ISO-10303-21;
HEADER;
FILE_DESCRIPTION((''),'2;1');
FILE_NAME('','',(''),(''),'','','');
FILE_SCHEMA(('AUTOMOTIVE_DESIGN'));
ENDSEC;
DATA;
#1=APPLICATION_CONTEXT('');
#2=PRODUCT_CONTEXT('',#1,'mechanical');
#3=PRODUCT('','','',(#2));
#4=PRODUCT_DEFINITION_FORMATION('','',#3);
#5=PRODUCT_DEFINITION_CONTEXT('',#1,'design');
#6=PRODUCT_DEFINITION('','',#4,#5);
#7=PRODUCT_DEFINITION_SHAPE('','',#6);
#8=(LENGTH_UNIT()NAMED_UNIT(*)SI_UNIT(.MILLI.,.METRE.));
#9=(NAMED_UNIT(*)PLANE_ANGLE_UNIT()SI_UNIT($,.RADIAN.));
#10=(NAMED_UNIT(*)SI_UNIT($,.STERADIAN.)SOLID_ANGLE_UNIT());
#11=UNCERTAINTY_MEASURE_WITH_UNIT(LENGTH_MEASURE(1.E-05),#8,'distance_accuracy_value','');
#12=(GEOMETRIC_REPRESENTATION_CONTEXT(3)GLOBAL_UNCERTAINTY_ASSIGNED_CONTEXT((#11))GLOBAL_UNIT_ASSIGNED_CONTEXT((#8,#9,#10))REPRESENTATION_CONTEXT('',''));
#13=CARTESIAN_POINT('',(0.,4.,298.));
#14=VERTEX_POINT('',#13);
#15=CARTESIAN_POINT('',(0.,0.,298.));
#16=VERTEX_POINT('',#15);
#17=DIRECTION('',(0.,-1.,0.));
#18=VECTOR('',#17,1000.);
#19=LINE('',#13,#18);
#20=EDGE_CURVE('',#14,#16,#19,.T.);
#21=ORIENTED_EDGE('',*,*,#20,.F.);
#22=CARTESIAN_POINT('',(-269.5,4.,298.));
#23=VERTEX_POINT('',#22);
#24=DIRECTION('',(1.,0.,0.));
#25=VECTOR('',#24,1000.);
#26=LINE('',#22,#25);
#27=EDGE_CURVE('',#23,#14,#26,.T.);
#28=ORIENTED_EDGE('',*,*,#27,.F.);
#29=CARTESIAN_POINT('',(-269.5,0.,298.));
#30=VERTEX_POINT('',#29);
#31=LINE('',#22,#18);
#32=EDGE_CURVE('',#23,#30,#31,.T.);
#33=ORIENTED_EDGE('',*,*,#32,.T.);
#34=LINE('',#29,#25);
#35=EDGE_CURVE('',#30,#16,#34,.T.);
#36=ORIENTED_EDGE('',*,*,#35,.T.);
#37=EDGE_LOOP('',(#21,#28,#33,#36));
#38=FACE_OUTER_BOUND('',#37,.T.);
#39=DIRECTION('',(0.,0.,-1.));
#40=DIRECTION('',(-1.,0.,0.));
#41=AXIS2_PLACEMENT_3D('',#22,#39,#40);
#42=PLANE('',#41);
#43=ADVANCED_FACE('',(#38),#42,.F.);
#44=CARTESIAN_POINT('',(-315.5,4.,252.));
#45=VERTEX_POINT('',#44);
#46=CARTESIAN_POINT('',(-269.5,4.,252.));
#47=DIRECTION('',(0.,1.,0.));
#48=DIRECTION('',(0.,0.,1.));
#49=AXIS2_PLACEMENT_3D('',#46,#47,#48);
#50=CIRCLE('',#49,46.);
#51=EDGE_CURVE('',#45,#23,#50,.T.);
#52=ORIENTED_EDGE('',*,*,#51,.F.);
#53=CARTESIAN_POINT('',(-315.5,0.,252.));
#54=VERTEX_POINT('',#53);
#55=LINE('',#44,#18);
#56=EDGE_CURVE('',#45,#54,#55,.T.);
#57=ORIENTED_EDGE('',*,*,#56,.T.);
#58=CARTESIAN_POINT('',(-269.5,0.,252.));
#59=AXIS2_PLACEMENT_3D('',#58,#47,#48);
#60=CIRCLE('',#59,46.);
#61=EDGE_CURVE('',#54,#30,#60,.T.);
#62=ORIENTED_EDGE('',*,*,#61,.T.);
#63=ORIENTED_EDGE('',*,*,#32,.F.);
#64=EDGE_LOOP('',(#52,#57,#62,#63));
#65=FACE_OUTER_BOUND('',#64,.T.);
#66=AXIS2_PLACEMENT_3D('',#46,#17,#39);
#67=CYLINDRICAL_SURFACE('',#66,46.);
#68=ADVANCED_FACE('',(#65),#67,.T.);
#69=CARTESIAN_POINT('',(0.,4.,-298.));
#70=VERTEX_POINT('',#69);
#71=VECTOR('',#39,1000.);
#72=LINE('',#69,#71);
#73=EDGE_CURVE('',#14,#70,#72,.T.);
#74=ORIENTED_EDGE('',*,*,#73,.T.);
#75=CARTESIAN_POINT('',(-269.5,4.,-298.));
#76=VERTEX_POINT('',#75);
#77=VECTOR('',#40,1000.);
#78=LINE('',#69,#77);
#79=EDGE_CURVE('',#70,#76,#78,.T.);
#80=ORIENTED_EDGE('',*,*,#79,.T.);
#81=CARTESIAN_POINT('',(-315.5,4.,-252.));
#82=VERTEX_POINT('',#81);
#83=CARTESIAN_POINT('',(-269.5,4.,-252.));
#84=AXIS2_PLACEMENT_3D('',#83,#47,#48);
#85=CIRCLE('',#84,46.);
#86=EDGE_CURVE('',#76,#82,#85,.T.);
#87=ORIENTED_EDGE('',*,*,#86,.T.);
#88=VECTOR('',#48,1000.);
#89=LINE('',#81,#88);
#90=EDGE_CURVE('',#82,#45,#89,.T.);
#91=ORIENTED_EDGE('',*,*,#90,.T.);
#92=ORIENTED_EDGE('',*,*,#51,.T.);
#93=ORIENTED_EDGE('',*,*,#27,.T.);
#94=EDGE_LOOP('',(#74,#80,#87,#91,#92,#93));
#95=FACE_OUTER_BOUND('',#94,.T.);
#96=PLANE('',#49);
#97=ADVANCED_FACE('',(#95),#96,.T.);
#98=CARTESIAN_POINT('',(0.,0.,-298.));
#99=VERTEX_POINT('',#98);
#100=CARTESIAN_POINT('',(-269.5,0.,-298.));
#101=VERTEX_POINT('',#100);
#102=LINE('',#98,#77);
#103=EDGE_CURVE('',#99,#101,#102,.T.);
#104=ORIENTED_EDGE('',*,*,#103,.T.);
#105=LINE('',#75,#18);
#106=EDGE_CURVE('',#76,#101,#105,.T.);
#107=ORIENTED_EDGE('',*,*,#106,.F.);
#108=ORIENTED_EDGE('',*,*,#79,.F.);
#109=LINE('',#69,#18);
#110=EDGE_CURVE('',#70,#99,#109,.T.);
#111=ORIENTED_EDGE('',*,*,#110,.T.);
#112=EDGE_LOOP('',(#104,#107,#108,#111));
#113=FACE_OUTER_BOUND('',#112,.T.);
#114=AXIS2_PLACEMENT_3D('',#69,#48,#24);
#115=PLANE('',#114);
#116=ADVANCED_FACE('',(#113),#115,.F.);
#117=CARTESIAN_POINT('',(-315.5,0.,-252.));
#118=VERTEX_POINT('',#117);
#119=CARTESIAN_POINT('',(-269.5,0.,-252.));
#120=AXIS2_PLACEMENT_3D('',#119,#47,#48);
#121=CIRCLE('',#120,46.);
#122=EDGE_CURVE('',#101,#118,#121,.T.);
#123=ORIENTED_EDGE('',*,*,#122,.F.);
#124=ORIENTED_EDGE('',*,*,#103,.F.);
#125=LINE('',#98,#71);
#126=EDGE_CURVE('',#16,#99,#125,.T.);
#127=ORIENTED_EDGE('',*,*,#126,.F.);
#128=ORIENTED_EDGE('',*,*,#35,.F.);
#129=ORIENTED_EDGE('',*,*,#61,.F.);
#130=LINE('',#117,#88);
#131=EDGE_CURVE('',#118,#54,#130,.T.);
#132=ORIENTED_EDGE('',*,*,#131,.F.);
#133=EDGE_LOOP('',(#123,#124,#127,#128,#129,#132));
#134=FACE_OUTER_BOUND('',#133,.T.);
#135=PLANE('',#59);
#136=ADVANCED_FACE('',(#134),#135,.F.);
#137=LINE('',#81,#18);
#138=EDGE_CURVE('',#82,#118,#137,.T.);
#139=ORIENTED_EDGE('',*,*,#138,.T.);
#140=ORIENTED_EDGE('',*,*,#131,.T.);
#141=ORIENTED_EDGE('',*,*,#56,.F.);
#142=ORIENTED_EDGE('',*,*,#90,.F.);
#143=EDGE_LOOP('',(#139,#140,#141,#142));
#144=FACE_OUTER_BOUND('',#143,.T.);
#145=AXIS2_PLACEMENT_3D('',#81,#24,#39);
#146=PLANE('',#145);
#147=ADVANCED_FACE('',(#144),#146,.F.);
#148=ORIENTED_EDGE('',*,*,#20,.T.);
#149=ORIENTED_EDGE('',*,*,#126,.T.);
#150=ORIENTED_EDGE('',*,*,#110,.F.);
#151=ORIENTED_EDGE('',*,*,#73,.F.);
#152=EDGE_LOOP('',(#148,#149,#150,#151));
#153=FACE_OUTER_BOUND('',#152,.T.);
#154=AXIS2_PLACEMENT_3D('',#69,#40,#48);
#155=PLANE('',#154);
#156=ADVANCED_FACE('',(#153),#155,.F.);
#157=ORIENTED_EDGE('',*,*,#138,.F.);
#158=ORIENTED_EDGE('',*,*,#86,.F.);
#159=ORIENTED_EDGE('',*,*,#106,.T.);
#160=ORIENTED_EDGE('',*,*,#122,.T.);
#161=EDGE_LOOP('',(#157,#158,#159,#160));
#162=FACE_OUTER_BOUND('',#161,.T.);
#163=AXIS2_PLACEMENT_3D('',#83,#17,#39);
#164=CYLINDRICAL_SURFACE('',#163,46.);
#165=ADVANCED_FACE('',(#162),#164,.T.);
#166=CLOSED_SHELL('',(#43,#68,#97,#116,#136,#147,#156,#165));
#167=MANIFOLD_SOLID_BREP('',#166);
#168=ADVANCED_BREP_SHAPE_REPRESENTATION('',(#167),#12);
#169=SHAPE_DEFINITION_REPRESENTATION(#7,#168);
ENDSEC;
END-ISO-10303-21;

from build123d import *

# Parameters (mm, degrees)
BOSS_EXTRUDE1_DEPTH = 4


with BuildPart() as part:
    # Sketch1 → Boss-Extrude1 (new body)
    with BuildSketch(Plane(origin=(0, 0, 0), x_dir=(1, 0, 0), z_dir=(0, 1, 0))):
        with BuildLine():
            Line((0, 298), (-269.5, 298))
            ThreePointArc((-269.5, 298), (-302.026911935, 284.526911935), (-315.5, 252))
            Line((-315.5, 252), (-315.5, -252))
            ThreePointArc((-315.5, -252), (-302.026911935, -284.526911935), (-269.5, -298))
            Line((-269.5, -298), (0, -298))
            Line((0, -298), (0, 298))
        make_face()
    extrude(amount=BOSS_EXTRUDE1_DEPTH)


solid = part.part
